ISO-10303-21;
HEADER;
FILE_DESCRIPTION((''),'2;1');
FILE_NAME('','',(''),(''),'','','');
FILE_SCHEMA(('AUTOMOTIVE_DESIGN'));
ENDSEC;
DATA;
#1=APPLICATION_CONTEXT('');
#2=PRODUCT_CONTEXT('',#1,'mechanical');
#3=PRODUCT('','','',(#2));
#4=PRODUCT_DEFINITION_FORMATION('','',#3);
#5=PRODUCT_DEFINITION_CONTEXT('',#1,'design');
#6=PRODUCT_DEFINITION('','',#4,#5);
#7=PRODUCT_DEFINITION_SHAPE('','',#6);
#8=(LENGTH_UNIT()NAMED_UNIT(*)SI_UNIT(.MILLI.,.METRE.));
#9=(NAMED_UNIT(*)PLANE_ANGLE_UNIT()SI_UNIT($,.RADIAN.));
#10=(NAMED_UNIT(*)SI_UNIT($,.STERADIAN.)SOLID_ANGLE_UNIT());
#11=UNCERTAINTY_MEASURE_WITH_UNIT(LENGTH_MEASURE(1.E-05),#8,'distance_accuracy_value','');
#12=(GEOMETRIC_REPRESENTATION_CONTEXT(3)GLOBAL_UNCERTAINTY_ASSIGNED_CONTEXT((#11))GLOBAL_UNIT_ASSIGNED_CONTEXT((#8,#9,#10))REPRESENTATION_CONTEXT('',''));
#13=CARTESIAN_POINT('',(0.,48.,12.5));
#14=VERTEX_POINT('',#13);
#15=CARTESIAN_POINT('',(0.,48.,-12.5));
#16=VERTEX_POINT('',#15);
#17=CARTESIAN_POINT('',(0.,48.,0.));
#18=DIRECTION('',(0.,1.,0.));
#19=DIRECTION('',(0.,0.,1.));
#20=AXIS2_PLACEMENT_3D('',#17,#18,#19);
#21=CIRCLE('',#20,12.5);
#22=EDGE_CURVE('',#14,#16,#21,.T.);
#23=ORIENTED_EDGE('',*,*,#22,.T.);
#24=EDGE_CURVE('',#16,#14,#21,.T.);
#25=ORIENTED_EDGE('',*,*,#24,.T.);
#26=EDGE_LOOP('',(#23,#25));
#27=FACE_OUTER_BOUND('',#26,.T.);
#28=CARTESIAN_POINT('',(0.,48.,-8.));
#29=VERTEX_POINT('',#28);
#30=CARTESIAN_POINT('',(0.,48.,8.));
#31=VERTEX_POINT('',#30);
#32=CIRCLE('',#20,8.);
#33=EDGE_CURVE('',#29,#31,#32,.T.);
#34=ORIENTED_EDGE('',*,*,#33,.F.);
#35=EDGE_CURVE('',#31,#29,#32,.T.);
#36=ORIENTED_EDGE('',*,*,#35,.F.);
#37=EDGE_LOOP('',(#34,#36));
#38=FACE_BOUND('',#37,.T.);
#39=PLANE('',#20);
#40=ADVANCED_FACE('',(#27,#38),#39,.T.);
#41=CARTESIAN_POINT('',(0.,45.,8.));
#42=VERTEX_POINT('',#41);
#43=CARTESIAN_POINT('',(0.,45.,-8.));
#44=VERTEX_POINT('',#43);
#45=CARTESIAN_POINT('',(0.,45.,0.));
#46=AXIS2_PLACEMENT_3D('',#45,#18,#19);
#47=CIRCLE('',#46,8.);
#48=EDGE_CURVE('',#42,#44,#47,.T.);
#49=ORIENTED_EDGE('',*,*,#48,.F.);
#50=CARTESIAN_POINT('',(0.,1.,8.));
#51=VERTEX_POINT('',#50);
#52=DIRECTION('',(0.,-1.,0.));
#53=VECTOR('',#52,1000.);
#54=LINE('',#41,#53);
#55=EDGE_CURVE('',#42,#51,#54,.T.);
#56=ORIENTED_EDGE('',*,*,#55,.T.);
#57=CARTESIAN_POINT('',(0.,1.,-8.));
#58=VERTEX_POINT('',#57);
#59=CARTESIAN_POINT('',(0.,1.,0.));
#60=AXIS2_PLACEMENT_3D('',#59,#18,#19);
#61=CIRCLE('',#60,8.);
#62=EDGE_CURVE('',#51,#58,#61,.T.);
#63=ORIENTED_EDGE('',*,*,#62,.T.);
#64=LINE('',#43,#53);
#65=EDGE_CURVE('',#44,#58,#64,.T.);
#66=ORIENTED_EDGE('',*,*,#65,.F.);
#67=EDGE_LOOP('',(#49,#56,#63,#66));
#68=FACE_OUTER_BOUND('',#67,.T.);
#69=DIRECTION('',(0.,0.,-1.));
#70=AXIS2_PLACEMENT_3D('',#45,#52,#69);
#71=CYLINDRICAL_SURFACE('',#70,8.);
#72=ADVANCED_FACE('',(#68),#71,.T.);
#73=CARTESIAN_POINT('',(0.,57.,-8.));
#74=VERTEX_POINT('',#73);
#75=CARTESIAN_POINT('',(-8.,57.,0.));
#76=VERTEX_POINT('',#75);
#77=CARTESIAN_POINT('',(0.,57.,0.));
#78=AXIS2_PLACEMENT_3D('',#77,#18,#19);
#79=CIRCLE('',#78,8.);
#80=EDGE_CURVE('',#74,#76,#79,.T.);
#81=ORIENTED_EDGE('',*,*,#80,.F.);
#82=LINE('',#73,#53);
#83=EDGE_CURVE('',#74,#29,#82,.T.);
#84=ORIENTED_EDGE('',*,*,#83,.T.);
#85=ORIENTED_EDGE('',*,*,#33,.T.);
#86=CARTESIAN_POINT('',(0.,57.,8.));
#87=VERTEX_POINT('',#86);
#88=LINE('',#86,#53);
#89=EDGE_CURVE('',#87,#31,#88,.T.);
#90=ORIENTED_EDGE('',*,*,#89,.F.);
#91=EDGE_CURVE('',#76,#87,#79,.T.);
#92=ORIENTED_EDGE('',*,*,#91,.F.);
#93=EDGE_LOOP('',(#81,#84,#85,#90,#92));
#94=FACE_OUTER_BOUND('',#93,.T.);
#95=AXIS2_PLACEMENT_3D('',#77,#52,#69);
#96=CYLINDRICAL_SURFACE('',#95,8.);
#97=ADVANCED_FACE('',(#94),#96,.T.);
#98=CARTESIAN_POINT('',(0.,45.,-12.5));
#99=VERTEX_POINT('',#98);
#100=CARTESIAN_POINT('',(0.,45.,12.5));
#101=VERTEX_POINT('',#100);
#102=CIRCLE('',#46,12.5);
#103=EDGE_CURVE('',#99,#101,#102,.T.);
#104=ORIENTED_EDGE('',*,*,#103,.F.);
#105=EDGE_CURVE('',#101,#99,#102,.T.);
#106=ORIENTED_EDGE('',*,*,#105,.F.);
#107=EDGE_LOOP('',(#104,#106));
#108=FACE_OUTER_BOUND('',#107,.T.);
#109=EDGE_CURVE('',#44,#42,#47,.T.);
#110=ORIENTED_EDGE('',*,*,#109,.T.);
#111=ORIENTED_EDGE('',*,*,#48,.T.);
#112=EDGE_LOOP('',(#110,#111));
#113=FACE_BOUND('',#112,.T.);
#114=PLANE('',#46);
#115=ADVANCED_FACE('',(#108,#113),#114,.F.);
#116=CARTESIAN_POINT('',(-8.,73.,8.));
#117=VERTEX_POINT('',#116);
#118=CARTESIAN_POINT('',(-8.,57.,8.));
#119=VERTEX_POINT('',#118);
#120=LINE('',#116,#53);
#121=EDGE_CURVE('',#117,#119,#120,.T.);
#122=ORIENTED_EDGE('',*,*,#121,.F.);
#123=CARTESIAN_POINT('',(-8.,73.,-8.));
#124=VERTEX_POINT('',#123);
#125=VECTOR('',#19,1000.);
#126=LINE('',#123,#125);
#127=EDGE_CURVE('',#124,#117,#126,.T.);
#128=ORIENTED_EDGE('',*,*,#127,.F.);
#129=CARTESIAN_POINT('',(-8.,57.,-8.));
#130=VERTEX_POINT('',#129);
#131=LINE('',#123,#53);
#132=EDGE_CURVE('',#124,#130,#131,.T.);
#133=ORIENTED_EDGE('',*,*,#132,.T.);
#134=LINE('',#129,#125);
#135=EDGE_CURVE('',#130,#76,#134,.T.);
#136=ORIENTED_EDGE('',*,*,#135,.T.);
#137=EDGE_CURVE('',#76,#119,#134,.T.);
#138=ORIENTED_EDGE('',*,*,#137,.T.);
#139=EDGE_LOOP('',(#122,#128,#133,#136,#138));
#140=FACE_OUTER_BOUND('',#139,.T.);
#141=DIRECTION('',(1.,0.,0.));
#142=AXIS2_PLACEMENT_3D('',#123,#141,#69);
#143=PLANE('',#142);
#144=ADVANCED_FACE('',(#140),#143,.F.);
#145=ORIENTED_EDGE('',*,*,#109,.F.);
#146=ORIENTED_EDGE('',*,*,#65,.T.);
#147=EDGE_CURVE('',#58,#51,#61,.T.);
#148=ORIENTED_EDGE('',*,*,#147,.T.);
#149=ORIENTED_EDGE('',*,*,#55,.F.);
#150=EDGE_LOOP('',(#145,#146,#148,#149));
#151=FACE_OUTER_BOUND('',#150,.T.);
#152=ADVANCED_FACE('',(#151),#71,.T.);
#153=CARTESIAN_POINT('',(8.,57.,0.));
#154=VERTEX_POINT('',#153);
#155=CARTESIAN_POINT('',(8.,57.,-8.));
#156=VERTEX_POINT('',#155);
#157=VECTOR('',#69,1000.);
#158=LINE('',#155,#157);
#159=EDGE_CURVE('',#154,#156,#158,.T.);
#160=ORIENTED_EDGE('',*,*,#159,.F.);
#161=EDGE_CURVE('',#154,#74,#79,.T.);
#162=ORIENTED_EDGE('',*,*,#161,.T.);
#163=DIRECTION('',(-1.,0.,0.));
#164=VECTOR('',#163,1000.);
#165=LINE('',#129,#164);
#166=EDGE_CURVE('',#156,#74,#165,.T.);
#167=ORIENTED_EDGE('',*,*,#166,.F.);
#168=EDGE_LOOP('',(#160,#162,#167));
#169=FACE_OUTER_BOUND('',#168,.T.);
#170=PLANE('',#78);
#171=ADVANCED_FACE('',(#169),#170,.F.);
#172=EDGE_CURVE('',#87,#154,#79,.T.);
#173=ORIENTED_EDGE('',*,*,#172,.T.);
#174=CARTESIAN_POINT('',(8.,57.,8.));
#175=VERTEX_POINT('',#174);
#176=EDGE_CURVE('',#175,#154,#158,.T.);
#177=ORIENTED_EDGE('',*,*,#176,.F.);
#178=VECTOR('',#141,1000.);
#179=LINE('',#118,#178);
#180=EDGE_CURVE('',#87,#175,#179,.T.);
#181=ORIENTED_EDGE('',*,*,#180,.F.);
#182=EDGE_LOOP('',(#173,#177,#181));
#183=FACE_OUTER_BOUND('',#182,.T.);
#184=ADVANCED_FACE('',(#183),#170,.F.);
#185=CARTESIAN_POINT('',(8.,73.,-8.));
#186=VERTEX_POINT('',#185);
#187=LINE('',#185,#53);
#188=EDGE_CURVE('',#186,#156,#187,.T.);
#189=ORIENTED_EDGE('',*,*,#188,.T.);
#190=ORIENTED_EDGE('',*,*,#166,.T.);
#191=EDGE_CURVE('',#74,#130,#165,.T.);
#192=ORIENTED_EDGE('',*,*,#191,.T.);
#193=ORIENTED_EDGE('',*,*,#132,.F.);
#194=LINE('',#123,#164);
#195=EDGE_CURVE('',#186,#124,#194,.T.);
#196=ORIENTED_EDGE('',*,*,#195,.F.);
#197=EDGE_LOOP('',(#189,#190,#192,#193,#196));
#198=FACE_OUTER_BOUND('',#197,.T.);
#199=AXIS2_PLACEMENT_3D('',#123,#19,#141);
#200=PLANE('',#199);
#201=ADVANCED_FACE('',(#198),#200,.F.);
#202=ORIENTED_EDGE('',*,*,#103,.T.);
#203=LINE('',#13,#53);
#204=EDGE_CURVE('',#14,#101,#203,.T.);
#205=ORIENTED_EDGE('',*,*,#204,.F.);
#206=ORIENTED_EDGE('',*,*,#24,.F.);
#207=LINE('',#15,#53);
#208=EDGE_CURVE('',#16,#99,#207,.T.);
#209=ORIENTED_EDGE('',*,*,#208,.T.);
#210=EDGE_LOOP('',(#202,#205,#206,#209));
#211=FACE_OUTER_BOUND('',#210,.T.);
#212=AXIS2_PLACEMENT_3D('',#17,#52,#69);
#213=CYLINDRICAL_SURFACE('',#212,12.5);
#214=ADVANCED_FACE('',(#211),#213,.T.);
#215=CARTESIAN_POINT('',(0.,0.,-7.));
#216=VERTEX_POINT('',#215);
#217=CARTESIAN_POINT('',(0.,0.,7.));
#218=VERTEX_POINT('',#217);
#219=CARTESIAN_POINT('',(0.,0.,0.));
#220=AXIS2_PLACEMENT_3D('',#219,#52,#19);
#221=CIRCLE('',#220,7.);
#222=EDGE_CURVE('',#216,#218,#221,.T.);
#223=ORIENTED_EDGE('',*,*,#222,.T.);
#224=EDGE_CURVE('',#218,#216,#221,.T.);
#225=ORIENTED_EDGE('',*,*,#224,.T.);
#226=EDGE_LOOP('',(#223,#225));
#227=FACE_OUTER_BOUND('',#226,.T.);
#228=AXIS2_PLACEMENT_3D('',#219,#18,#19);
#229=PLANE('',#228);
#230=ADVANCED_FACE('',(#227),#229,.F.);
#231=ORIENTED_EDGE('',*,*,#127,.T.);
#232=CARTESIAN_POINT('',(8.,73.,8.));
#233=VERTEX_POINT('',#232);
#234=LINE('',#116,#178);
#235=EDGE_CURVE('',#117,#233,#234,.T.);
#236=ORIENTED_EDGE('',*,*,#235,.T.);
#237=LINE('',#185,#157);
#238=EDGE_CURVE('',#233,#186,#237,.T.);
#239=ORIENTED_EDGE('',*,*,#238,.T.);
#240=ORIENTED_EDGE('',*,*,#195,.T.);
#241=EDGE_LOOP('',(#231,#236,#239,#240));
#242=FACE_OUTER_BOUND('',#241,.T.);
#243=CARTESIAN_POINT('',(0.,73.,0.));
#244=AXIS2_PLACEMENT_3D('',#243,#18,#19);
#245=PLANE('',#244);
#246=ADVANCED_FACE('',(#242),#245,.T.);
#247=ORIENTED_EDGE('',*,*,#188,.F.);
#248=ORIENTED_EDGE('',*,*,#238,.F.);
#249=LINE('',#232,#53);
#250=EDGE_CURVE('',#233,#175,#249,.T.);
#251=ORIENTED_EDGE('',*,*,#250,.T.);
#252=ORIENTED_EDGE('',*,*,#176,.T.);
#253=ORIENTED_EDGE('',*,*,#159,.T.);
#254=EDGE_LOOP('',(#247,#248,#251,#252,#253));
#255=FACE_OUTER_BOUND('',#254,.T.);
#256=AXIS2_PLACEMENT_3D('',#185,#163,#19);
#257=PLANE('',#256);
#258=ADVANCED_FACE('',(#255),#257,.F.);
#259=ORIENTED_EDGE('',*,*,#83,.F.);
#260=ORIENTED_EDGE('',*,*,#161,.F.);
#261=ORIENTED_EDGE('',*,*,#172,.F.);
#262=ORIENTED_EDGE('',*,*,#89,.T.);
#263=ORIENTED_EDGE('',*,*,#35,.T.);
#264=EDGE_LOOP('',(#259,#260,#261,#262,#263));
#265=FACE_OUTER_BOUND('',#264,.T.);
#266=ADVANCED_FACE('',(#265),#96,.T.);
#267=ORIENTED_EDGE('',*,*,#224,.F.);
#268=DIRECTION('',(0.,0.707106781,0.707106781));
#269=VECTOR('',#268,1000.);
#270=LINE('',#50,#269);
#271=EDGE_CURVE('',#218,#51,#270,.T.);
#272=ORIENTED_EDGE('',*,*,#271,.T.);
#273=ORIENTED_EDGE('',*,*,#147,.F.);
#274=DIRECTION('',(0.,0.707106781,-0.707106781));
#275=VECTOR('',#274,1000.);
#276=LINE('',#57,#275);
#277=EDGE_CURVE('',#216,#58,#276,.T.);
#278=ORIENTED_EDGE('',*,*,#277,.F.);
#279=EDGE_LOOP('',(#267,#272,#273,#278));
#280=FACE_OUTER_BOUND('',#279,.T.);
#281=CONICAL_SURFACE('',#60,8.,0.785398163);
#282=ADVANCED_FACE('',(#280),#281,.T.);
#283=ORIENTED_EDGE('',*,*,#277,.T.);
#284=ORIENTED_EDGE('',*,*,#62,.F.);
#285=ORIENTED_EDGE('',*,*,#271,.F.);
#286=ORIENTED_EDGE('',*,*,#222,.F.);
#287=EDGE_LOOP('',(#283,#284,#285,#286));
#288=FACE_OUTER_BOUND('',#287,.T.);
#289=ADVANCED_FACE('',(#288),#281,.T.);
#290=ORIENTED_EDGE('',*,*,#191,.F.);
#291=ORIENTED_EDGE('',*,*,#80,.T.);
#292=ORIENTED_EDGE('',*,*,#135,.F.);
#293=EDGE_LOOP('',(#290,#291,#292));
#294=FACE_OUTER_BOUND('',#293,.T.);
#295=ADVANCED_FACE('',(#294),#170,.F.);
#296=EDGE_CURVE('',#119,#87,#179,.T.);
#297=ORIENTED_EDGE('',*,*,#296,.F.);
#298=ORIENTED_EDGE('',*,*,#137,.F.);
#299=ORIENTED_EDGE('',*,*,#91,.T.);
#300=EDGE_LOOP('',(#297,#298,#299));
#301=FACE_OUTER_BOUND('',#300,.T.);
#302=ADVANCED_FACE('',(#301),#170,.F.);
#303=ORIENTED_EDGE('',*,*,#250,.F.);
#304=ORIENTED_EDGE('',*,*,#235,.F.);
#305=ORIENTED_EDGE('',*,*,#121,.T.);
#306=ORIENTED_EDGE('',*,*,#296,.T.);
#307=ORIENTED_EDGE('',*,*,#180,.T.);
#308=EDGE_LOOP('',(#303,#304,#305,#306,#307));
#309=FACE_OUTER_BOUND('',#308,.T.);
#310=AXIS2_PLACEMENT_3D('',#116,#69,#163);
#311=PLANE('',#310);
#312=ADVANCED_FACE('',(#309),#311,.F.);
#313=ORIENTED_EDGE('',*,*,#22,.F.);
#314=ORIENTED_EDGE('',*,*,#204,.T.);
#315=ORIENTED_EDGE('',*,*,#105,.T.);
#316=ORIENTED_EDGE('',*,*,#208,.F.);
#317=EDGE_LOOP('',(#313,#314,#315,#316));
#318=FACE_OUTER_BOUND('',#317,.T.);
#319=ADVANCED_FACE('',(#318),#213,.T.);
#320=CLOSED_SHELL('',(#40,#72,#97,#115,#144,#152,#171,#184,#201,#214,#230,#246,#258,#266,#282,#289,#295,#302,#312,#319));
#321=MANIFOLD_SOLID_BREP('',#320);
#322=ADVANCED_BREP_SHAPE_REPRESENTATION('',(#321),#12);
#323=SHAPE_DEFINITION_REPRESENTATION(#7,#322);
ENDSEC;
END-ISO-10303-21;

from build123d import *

# Parameters (mm, degrees)
SHANK_SKETCH_16_R          = 8
SHANK_16X45_DEPTH          = 45
SHANK_CHAMFER_1X45_SIZE    = 1
COLLAR_SKETCH_25_R         = 12.5
COLLAR_25X3_DEPTH          = 3
NECK_SKETCH_16_R           = 8
NECK_16X9_DEPTH            = 9
SQUARE_HEAD_SKETCH_16X16_W = 16
SQUARE_HEAD_SKETCH_16X16_H = 16
SQUARE_HEAD_16X16X16_DEPTH = 16


with BuildPart() as part:
    # Shank Sketch Ø16 → Shank Ø16x45 (new body)
    with BuildSketch(Plane(origin=(0, 0, 0), x_dir=(1, 0, 0), z_dir=(0, 1, 0))):
        with Locations(Location((0, 0, 0), (0, 0, 90))):
            Circle(SHANK_SKETCH_16_R)
    extrude(amount=SHANK_16X45_DEPTH)

    # Shank Chamfer 1x45°
    shank_chamfer_1x45_edges = [part.edges().sort_by_distance(p)[0] for p in [
        (0, 0, 8),
    ]]
    chamfer(shank_chamfer_1x45_edges, length=SHANK_CHAMFER_1X45_SIZE)

    # Collar Sketch Ø25 → Collar Ø25x3 (add)
    with BuildSketch(Plane(origin=(0, 45, 0), x_dir=(1, 0, 0), z_dir=(0, 1, 0))):
        with Locations(Location((0, 0, 0), (0, 0, 270))):
            Circle(COLLAR_SKETCH_25_R)
    extrude(amount=COLLAR_25X3_DEPTH)

    # Neck Sketch Ø16 → Neck Ø16x9 (add)
    with BuildSketch(Plane(origin=(0, 48, 0), x_dir=(1, 0, 0), z_dir=(0, 1, 0))):
        with Locations(Location((0, 0, 0), (0, 0, 90))):
            Circle(NECK_SKETCH_16_R)
    extrude(amount=NECK_16X9_DEPTH)

    # Square Head Sketch 16x16 → Square Head 16x16x16 (add)
    with BuildSketch(Plane(origin=(0, 57, 0), x_dir=(1, 0, 0), z_dir=(0, 1, 0))):
        Rectangle(SQUARE_HEAD_SKETCH_16X16_W, SQUARE_HEAD_SKETCH_16X16_H)
    extrude(amount=SQUARE_HEAD_16X16X16_DEPTH)


solid = part.part
